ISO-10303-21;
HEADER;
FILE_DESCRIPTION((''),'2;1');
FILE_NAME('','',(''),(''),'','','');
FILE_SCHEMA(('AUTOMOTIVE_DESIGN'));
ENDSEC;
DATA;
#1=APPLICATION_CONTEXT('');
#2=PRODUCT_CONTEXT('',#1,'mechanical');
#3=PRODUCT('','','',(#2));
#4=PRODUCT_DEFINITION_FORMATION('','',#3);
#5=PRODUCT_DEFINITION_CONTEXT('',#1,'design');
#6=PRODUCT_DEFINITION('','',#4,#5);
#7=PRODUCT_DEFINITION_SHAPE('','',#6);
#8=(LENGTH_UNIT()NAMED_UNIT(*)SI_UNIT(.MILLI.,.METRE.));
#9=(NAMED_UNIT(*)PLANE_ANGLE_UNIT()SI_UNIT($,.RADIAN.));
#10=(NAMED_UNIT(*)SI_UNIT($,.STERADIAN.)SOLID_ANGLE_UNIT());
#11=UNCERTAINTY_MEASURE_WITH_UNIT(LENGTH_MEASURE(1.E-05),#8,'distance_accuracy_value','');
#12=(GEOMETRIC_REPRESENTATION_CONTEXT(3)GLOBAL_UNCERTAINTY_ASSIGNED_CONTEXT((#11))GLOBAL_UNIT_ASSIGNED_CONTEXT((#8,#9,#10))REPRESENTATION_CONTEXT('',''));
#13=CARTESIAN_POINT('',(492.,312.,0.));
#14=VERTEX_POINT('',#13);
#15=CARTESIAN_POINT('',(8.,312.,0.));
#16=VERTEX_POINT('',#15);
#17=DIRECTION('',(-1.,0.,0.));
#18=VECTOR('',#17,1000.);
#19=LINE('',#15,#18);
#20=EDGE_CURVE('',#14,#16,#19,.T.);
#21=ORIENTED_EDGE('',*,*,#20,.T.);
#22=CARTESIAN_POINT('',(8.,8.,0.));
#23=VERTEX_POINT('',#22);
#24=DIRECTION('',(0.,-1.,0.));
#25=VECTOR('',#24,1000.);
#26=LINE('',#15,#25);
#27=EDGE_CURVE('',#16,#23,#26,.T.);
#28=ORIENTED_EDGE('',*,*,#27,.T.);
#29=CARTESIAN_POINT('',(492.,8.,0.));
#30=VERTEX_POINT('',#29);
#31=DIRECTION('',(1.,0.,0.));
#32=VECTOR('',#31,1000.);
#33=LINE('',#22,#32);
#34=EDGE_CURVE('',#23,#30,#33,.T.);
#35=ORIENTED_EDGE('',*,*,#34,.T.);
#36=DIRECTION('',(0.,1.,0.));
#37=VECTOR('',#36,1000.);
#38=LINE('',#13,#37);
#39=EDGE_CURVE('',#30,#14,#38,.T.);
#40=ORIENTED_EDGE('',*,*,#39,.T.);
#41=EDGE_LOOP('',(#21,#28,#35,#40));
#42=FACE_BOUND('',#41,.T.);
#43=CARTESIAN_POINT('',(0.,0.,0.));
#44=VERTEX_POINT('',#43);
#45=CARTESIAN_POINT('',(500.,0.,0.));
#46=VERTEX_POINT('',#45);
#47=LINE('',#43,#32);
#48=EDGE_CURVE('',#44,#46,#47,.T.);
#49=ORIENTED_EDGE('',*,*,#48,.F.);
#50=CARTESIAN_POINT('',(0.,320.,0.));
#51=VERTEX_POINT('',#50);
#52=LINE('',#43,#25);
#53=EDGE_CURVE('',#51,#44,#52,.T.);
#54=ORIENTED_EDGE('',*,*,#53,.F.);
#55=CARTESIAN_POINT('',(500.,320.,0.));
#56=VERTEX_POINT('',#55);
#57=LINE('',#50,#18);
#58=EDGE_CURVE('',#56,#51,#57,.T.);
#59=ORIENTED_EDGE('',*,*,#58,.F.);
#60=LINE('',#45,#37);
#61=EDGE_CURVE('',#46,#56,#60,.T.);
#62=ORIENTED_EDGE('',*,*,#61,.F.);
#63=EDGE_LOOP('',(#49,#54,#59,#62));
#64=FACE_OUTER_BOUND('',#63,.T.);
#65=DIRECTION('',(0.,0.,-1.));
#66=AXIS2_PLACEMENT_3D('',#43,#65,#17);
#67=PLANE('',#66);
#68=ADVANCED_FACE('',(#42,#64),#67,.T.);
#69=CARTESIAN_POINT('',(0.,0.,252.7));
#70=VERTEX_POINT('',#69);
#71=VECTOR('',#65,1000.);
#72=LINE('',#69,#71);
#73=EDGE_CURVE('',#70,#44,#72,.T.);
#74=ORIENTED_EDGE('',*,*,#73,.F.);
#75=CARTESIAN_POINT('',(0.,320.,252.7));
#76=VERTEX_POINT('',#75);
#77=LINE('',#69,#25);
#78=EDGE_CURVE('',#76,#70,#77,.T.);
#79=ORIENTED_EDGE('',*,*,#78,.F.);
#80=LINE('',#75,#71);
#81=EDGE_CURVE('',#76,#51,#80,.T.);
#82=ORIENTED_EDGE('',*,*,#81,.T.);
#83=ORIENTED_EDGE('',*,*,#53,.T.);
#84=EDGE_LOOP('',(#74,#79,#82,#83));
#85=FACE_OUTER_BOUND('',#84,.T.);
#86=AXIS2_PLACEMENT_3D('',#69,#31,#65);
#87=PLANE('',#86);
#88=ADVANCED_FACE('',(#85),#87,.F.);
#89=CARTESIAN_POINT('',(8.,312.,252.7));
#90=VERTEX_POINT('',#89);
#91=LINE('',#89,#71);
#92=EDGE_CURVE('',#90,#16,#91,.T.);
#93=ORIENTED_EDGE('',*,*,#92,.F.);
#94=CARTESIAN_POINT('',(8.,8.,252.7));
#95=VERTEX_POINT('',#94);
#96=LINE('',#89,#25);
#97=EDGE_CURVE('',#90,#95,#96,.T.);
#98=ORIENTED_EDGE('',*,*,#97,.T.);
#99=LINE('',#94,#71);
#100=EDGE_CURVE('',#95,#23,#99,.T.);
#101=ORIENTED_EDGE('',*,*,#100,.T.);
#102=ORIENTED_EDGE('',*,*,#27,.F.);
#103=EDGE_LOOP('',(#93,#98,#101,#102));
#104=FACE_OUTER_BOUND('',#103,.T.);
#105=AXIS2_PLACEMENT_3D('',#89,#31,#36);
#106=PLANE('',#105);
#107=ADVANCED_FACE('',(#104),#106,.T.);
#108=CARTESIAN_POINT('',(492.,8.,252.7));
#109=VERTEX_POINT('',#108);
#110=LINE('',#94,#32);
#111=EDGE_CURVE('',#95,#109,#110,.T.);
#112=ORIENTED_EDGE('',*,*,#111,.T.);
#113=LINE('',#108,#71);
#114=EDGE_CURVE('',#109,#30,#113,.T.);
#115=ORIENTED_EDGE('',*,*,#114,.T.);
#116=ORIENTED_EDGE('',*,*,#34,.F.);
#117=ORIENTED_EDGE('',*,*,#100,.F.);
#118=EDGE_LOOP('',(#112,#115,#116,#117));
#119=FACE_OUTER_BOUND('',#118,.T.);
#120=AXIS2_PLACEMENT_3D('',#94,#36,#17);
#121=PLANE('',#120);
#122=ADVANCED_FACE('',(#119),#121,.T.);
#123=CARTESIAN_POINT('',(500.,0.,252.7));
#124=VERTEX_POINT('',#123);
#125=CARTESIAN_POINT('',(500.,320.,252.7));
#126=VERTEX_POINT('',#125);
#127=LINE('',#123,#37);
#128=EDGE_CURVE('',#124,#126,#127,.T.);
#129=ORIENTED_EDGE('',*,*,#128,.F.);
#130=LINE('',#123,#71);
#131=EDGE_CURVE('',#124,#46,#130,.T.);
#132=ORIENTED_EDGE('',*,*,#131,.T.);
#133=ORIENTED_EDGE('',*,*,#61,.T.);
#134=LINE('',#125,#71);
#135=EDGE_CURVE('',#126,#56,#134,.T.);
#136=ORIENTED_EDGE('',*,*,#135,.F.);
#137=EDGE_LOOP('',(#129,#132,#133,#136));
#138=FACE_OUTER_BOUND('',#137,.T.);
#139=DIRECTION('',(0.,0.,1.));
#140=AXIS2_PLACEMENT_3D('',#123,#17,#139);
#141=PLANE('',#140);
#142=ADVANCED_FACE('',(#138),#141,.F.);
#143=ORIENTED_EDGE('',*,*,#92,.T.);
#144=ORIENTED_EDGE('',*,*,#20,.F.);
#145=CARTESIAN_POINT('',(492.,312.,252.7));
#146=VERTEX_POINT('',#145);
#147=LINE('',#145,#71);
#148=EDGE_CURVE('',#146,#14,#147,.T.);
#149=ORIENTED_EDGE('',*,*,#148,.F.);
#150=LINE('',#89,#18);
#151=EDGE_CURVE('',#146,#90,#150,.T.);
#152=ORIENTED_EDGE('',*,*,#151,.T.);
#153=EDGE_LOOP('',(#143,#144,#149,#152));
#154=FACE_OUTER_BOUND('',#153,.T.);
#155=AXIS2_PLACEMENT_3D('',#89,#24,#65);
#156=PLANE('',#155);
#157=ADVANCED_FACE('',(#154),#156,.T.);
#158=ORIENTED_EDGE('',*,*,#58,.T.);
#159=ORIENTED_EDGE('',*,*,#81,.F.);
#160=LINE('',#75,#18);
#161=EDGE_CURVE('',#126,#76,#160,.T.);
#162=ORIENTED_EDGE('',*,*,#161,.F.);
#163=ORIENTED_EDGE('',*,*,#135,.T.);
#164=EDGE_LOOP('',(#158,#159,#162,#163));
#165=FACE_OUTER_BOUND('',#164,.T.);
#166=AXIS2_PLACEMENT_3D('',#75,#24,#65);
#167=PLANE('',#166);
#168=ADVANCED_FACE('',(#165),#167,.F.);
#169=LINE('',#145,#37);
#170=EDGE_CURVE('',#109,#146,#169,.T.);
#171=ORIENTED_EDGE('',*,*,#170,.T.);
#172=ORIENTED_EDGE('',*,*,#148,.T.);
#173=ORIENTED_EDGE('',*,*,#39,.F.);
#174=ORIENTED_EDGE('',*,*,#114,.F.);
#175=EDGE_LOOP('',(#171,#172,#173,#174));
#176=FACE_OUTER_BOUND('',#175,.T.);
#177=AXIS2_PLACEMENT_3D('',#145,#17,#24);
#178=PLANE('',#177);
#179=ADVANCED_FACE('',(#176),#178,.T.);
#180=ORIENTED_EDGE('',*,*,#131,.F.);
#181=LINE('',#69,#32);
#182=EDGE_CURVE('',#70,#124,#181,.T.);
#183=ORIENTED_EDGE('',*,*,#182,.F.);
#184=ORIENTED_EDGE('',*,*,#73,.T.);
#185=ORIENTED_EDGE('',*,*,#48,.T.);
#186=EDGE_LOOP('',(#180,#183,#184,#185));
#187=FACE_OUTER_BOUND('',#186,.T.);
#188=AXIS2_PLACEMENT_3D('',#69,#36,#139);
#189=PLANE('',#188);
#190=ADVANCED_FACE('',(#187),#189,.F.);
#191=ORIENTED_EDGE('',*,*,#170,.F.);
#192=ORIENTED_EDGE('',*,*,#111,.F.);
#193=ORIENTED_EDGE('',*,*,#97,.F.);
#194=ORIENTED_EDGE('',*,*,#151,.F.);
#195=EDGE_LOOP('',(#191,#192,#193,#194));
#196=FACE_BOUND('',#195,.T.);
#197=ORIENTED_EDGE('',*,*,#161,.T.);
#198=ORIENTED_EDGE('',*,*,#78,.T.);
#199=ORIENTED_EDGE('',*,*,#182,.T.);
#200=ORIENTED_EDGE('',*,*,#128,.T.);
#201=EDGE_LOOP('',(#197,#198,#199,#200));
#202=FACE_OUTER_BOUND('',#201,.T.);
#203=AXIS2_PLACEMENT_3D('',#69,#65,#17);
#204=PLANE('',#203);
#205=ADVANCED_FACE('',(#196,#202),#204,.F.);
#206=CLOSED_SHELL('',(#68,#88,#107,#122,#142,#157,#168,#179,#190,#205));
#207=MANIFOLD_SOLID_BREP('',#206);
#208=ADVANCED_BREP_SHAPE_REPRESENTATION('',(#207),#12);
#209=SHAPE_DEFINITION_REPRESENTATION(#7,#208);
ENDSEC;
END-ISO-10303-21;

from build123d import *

# Parameters (mm, degrees)
SKETCH1_W           = 500
SKETCH1_H           = 320
SKETCH1_W_2         = 484
SKETCH1_H_2         = 304
BOSS_EXTRUDE1_DEPTH = 252.7


with BuildPart() as part:
    # Sketch1 → Boss-Extrude1 (new body)
    with BuildSketch(Plane.XY):
        with Locations((250, 160)):
            Rectangle(SKETCH1_W, SKETCH1_H)
        with Locations((250, 160)):
            Rectangle(SKETCH1_W_2, SKETCH1_H_2, mode=Mode.SUBTRACT)
    extrude(amount=BOSS_EXTRUDE1_DEPTH)


solid = part.part
